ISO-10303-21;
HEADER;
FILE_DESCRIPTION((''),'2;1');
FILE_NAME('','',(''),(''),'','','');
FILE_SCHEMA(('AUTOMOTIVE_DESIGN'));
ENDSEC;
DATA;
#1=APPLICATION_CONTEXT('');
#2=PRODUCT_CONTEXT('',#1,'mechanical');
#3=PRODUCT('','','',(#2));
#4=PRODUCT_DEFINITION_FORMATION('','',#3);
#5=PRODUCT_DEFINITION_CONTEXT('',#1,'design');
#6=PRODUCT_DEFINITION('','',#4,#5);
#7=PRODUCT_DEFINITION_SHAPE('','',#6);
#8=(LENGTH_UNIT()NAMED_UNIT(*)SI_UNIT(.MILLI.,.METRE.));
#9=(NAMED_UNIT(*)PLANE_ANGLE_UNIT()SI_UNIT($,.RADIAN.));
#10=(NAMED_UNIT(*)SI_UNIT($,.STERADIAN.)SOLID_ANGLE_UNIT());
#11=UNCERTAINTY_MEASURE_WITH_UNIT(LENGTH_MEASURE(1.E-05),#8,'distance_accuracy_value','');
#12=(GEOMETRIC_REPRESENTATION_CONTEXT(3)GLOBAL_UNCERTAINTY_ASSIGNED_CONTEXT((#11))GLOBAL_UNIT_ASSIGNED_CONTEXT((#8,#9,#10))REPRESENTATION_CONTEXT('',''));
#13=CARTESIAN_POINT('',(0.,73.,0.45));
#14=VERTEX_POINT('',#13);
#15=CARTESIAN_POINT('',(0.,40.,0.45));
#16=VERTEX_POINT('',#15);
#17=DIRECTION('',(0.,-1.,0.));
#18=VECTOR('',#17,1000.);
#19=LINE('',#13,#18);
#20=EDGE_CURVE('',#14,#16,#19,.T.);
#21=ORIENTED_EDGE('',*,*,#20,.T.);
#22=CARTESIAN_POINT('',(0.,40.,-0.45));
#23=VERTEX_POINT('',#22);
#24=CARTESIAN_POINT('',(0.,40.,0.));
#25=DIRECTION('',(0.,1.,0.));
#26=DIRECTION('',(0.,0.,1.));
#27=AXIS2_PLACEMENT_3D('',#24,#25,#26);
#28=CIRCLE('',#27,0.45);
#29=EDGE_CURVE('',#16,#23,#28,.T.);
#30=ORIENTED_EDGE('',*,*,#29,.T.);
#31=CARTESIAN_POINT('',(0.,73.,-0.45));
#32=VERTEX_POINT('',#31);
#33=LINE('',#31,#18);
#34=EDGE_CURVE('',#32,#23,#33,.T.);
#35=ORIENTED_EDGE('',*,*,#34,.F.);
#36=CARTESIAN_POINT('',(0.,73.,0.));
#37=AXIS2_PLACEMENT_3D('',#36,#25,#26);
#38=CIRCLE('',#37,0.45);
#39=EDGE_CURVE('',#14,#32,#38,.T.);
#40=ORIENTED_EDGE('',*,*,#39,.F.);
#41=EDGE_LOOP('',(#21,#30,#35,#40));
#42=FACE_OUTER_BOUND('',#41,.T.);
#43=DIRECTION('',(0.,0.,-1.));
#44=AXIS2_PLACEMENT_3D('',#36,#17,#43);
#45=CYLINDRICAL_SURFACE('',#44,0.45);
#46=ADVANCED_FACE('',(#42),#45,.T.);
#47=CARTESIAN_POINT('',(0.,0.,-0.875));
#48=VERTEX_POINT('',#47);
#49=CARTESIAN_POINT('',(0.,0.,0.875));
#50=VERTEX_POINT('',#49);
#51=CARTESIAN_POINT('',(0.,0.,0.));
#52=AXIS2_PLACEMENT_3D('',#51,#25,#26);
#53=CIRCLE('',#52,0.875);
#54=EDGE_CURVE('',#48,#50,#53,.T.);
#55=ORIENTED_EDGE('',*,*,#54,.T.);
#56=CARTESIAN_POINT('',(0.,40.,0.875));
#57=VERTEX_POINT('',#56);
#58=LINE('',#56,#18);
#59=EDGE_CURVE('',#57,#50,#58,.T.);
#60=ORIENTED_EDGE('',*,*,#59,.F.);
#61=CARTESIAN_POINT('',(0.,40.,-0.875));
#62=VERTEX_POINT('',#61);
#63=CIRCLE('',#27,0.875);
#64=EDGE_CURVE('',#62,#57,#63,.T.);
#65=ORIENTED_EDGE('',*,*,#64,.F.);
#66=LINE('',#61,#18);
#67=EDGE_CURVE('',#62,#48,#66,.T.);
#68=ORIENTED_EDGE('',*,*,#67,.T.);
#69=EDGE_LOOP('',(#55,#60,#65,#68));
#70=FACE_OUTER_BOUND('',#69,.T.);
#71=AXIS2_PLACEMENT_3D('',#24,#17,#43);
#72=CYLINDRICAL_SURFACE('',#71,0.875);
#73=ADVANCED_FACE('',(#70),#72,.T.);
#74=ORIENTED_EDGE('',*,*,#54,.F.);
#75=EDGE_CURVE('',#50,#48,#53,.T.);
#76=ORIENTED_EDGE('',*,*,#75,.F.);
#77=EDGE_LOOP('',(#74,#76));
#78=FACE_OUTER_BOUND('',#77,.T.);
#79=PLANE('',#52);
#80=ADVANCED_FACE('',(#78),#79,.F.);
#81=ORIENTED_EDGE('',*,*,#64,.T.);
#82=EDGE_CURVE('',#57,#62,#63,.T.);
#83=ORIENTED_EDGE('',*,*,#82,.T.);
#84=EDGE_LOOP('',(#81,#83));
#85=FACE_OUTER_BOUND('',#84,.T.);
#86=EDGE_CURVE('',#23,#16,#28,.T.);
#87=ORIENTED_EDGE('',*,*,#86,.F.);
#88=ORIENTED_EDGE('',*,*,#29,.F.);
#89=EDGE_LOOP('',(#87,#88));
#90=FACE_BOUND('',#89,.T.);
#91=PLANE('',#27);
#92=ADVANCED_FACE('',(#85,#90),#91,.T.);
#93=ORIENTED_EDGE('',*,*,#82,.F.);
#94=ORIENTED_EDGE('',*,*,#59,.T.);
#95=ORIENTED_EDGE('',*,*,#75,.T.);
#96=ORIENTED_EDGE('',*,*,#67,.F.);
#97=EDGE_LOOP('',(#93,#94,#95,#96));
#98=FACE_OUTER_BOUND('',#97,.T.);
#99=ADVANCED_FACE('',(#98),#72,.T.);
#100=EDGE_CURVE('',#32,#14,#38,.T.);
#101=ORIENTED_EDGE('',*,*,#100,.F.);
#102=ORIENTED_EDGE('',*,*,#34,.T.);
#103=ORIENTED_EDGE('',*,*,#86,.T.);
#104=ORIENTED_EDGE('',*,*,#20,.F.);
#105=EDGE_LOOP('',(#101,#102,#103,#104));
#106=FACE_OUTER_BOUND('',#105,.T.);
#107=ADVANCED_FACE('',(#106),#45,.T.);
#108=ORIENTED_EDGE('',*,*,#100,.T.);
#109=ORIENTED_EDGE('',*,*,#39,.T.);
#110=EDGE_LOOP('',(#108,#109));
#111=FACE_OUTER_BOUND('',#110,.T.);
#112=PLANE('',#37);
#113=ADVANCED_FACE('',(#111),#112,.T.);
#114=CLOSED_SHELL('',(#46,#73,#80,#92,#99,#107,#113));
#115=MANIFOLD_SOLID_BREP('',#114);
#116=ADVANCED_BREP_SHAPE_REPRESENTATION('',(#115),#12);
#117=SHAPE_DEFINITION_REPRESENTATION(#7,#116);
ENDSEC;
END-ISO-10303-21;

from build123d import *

# Parameters (mm, degrees)
SKETCH1_R           = 0.875
BOSS_EXTRUDE1_DEPTH = 40
SKETCH2_R           = 0.45
BOSS_EXTRUDE2_DEPTH = 33


with BuildPart() as part:
    # Sketch1 → Boss-Extrude1 (new body)
    with BuildSketch(Plane(origin=(0, 0, 0), x_dir=(1, 0, 0), z_dir=(0, 1, 0))):
        with Locations(Location((0, 0, 0), (0, 0, 270))):
            Circle(SKETCH1_R)
    extrude(amount=BOSS_EXTRUDE1_DEPTH)

    # Sketch2 → Boss-Extrude2 (add)
    with BuildSketch(Plane(origin=(0, 40, 0), x_dir=(1, 0, 0), z_dir=(0, 1, 0))):
        with Locations(Location((0, 0, 0), (0, 0, 270))):
            Circle(SKETCH2_R)
    extrude(amount=BOSS_EXTRUDE2_DEPTH)


solid = part.part
